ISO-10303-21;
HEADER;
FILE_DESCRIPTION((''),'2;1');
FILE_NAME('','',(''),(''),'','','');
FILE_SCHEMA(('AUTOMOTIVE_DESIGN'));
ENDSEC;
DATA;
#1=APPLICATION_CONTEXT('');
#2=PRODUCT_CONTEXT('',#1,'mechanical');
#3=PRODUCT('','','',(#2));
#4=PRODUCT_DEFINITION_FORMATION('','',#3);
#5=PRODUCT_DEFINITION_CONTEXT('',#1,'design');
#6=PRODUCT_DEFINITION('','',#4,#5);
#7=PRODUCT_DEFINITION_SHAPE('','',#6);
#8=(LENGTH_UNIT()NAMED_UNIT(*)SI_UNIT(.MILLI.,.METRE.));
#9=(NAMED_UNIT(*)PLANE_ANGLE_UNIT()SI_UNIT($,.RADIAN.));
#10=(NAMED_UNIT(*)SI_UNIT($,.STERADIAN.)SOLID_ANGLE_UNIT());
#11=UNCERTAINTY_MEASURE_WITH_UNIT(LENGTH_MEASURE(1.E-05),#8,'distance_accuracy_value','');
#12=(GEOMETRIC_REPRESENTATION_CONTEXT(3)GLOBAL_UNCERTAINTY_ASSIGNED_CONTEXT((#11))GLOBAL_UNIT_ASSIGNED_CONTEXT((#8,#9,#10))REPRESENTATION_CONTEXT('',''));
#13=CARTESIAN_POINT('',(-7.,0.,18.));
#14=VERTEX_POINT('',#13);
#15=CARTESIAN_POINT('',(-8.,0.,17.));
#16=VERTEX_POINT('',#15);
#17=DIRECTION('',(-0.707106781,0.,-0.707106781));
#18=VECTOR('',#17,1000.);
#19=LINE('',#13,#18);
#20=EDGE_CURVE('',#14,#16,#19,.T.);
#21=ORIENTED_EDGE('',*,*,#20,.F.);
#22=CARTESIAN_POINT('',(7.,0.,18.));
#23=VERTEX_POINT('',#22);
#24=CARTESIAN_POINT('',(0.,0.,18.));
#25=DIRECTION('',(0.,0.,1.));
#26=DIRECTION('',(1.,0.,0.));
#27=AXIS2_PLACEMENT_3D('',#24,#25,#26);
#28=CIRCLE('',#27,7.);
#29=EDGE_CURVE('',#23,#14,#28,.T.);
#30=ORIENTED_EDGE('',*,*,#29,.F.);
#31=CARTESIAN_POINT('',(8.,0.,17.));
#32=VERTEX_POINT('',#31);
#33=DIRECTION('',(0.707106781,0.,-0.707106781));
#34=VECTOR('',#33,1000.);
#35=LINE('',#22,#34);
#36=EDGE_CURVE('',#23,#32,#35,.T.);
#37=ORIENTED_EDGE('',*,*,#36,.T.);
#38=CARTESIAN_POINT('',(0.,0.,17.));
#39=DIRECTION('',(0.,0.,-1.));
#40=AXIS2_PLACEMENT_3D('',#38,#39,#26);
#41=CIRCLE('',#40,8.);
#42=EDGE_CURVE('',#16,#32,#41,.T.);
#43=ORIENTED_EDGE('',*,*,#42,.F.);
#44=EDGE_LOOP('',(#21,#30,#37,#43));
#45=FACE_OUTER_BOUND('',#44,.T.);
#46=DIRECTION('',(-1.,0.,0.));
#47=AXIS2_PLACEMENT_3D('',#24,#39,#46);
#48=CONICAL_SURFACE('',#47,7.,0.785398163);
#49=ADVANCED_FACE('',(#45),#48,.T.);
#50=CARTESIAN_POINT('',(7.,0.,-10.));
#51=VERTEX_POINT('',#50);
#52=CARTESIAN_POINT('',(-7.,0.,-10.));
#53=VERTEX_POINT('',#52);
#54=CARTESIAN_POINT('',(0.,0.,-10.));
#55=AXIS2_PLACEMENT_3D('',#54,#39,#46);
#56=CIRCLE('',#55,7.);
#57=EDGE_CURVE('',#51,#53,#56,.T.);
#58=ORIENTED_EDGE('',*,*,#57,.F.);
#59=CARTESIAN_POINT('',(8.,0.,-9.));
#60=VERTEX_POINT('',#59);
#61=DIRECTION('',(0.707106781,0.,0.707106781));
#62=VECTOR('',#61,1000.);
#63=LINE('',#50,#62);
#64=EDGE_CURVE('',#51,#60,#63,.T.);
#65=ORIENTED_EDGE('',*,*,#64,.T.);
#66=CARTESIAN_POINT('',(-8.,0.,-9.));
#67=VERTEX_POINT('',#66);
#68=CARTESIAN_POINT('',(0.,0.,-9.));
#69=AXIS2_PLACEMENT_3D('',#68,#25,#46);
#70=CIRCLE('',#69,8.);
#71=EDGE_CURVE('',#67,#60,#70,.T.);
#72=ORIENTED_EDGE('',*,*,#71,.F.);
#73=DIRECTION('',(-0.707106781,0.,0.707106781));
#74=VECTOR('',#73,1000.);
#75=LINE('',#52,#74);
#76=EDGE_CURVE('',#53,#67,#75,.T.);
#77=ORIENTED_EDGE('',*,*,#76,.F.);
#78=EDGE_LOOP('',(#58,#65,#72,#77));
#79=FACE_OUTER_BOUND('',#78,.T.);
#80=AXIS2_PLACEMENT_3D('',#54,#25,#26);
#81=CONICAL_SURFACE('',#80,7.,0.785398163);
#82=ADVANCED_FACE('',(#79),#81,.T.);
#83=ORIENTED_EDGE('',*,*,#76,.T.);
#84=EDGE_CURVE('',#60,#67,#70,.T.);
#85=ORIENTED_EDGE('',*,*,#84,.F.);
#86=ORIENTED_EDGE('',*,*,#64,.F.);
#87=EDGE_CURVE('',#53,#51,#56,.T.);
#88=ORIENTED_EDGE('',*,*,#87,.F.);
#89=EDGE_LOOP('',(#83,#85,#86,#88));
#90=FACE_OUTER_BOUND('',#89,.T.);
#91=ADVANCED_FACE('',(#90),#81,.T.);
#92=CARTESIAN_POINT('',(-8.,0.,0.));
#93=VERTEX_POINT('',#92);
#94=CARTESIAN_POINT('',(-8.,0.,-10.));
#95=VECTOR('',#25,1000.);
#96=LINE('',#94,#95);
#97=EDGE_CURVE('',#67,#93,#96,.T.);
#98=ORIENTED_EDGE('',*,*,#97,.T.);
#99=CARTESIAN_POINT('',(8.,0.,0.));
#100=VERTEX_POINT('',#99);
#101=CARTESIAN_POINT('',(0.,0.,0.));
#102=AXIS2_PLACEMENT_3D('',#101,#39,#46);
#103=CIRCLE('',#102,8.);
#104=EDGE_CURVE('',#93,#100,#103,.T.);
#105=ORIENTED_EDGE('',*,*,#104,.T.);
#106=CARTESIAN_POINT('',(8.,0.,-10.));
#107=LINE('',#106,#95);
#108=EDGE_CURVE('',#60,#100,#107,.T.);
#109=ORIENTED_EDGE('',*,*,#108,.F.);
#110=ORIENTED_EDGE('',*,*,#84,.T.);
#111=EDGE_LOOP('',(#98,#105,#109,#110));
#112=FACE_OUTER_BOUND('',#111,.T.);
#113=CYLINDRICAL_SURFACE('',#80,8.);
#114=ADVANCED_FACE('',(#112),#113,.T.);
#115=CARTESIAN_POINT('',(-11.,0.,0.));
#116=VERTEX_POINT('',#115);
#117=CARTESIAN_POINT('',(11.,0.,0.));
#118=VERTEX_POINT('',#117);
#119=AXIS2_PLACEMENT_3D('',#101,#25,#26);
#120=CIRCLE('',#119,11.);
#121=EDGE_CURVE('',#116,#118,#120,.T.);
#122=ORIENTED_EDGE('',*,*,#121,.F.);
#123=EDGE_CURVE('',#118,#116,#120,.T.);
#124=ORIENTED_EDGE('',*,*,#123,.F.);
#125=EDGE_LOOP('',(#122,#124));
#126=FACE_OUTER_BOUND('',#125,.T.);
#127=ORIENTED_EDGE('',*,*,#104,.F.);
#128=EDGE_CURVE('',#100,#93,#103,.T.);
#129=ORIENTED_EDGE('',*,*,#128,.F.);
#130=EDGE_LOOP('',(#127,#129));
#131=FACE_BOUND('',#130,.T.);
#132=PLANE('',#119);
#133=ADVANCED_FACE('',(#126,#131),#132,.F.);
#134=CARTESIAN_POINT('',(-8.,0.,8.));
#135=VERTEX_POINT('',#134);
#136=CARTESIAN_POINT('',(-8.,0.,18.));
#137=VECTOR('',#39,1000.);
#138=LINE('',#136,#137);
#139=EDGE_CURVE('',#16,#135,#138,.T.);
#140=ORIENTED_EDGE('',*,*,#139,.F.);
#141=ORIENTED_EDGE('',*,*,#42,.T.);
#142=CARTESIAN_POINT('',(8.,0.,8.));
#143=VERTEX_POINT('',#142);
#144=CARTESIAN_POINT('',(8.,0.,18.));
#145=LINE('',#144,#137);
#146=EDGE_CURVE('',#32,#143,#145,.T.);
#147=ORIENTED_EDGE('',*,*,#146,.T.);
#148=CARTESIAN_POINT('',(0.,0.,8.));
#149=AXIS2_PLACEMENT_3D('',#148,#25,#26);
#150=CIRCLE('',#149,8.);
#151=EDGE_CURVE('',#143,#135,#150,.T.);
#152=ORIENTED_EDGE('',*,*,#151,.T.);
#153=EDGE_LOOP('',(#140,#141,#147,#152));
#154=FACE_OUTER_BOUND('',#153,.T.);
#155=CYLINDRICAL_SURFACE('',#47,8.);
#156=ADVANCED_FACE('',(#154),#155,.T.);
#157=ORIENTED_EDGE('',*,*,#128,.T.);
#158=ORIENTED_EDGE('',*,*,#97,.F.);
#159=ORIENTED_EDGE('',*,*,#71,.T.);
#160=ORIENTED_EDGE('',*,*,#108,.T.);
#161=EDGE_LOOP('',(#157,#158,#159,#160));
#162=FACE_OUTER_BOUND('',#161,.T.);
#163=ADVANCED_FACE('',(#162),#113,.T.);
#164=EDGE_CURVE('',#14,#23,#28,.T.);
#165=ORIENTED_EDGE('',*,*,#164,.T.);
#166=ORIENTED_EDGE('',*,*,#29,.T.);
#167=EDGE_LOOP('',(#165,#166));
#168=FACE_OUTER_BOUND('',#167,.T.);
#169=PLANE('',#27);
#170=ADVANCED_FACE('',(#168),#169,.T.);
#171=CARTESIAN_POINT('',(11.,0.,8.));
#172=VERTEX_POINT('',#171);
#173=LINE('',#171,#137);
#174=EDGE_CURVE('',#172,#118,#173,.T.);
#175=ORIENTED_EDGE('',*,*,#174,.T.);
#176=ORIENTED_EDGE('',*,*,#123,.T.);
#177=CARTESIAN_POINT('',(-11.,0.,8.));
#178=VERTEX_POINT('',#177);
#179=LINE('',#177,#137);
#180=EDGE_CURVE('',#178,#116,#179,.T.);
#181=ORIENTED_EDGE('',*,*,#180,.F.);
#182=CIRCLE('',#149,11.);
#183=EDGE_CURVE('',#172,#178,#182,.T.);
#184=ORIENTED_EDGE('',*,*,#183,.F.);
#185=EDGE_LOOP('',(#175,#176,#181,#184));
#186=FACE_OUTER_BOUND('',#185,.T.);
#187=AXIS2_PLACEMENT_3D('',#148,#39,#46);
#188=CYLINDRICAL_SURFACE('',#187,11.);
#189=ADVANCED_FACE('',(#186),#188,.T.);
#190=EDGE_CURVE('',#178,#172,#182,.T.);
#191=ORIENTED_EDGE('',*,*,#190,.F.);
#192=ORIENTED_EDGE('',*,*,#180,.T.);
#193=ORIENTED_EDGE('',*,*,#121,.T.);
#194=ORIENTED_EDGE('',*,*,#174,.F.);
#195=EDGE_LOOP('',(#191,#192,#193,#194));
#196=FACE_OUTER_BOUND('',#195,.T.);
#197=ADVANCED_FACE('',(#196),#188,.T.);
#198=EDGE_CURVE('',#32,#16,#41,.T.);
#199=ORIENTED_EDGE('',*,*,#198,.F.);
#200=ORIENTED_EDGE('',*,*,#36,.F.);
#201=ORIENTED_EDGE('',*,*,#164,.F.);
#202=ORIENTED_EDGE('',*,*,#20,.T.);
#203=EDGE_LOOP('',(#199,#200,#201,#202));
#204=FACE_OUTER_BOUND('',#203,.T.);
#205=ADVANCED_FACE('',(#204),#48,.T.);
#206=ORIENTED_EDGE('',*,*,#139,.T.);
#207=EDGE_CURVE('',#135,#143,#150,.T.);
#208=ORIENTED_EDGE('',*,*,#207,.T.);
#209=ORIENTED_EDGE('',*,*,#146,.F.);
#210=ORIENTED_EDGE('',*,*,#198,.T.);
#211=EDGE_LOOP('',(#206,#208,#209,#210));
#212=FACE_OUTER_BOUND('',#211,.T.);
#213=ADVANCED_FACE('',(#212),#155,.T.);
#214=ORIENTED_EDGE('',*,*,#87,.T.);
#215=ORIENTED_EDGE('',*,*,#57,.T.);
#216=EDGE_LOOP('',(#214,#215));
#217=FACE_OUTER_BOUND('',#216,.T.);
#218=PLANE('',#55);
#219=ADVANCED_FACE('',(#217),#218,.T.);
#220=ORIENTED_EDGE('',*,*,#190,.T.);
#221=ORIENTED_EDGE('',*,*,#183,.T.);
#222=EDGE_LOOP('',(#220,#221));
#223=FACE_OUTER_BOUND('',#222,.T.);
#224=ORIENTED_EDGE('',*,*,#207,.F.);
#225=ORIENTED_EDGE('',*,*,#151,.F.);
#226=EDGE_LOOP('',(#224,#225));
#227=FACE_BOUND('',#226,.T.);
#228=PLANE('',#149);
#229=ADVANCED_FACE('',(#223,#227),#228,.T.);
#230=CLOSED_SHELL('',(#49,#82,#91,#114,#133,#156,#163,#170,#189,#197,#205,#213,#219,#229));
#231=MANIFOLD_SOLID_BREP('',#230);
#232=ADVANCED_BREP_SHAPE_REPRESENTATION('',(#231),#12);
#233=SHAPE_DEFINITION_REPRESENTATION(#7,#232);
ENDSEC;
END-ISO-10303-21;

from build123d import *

# Parameters (mm, degrees)
SKETCH1_R           = 11
BOSS_EXTRUDE1_DEPTH = 8
SKETCH2_R           = 8
BOSS_EXTRUDE2_DEPTH = 10
BOSS_EXTRUDE3_START = 10
SKETCH3_R           = 8
BOSS_EXTRUDE3_DEPTH = 10
CHAMFER1_SIZE       = 1


with BuildPart() as part:
    # Sketch1 → Boss-Extrude1 (new body)
    with BuildSketch(Plane.XY):
        Circle(SKETCH1_R)
    extrude(amount=BOSS_EXTRUDE1_DEPTH)

    # Sketch2 → Boss-Extrude2 (add)
    with BuildSketch(Plane.XY.offset(8)):
        Circle(SKETCH2_R)
    extrude(amount=BOSS_EXTRUDE2_DEPTH)

    # Sketch3 → Boss-Extrude3 (add)
    with BuildSketch(Plane(origin=(0, 0, 0), x_dir=(-1, 0, 0), z_dir=(0, 0, -1)).offset(BOSS_EXTRUDE3_START)):
        with Locations(Location((0, 0, 0), (0, 0, 180))):
            Circle(SKETCH3_R)
    extrude(amount=-BOSS_EXTRUDE3_DEPTH)

    # Chamfer1
    chamfer1_edges = [part.edges().sort_by_distance(p)[0] for p in [
        (-8, 0, -10),
        (-8, 0, 18),
    ]]
    chamfer(chamfer1_edges, length=CHAMFER1_SIZE)


solid = part.part
